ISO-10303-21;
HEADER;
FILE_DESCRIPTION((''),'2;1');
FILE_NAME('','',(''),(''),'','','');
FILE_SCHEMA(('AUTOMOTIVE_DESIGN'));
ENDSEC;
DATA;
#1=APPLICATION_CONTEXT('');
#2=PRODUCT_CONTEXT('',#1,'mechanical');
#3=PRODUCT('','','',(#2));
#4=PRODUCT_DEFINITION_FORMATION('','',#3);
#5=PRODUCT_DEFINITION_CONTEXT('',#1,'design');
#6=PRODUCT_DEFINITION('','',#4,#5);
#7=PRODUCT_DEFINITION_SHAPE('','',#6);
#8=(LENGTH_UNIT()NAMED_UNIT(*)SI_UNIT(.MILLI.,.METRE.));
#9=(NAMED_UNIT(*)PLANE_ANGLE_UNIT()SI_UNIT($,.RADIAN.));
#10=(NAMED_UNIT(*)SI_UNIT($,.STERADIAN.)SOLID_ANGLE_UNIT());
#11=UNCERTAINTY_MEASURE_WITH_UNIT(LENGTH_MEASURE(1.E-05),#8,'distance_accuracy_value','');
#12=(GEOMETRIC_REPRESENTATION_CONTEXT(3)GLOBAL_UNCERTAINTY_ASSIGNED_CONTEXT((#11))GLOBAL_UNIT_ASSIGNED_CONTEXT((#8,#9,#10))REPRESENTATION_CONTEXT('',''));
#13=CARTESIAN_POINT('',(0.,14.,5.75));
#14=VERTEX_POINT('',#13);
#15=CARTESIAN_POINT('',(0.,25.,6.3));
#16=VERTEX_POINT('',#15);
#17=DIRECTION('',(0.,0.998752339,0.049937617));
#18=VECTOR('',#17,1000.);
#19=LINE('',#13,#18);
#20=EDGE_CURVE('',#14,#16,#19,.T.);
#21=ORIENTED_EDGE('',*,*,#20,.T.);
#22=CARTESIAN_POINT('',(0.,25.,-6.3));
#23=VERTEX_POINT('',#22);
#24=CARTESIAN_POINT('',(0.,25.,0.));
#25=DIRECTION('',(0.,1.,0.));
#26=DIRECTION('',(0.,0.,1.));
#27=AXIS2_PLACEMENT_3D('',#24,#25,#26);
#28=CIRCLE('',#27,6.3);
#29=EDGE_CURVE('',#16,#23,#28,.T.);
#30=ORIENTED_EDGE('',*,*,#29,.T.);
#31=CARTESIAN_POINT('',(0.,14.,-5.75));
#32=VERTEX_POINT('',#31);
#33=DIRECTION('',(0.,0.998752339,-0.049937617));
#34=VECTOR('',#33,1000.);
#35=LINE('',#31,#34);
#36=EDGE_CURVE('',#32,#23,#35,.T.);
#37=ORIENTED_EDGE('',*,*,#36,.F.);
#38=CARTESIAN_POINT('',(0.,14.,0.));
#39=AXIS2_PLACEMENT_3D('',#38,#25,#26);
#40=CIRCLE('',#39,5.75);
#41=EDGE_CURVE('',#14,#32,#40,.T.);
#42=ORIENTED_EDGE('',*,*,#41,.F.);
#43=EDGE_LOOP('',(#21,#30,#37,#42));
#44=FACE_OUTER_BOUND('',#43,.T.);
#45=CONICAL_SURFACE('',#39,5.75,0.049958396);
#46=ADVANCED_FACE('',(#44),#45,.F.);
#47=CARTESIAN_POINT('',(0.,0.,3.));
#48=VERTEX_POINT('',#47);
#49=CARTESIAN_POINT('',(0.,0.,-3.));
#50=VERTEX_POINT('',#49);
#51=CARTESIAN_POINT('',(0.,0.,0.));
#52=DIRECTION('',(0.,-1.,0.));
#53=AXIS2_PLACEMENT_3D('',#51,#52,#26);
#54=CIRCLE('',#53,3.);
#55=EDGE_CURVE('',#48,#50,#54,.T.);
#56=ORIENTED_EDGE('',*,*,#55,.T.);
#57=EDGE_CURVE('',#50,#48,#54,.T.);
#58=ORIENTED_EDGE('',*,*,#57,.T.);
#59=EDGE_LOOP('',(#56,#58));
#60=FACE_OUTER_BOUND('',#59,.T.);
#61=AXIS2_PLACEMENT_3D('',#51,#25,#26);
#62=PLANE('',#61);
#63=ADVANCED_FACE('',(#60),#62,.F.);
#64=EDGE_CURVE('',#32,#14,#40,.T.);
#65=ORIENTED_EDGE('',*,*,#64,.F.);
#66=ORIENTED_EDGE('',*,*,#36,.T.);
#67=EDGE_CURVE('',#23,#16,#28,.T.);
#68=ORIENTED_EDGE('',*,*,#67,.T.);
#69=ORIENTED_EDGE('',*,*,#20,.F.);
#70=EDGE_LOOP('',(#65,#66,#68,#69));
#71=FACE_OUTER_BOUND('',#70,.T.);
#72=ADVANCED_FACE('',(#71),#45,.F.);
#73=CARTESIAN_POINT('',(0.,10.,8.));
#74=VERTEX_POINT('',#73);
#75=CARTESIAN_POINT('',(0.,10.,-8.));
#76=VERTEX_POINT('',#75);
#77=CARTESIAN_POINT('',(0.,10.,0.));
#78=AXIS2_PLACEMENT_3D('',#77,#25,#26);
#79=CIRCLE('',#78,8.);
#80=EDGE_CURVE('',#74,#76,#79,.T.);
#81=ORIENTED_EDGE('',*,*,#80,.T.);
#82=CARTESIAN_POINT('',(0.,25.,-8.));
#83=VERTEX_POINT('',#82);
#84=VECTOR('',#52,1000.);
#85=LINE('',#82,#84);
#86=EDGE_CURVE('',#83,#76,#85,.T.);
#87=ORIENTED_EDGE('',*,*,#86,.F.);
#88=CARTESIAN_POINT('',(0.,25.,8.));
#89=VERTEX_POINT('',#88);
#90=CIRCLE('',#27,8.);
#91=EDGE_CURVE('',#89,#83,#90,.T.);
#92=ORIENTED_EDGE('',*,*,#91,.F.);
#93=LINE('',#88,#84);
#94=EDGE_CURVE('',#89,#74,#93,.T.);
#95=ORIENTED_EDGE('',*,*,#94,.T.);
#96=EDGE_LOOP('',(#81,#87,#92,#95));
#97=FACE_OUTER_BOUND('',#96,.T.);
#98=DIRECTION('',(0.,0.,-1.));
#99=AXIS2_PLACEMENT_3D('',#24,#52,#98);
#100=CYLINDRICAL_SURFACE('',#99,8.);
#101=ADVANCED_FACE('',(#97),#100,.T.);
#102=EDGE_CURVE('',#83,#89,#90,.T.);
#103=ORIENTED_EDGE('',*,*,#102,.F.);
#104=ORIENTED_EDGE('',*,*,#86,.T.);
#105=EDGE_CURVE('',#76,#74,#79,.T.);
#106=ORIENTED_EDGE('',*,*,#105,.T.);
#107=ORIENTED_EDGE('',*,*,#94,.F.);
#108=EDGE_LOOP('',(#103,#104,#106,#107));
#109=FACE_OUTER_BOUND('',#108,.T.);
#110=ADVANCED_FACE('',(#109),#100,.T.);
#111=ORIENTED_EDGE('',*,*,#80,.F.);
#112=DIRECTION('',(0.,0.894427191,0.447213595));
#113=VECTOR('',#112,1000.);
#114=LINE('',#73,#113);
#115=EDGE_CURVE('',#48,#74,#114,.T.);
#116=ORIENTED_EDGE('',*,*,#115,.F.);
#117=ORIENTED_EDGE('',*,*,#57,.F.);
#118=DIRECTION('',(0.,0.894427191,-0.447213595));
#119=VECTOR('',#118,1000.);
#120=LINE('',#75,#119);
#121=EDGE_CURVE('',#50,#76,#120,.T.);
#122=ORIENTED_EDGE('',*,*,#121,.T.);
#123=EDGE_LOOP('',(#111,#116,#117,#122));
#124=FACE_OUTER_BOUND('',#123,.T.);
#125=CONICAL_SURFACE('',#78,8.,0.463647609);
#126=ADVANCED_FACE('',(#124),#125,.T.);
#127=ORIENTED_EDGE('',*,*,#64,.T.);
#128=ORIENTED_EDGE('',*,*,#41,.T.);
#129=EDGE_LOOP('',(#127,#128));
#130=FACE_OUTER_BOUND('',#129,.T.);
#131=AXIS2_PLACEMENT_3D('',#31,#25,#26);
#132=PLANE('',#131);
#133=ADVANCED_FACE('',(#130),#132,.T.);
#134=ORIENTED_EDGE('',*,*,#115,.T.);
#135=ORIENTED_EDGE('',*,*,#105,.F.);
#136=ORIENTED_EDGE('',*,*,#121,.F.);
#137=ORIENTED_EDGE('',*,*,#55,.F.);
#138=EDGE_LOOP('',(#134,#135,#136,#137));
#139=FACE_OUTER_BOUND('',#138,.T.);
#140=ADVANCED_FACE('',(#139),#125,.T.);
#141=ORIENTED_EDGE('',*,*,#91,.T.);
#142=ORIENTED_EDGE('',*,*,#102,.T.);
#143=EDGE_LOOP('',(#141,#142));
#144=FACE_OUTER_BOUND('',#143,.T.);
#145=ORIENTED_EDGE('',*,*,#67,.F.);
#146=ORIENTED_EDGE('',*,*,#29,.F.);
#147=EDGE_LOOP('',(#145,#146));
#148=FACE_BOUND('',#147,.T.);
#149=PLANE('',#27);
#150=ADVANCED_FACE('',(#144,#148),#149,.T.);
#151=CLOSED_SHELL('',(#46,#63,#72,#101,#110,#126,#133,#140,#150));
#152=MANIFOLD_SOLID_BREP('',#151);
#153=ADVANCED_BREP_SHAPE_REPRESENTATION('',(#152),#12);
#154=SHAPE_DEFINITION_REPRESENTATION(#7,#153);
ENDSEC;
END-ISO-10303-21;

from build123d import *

# Parameters (mm, degrees)
SKETCH_1_R      = 8
EXTRUDE_1_DEPTH = 25
CHAMFER_2_SIZE  = 5
CHAMFER_2_SIZE2 = 10


with BuildPart() as part:
    # 草图1 → 凸台-拉伸1 (new body)
    with BuildSketch(Plane(origin=(0, 0, 0), x_dir=(1, 0, 0), z_dir=(0, 1, 0))):
        with Locations(Location((0, 0, 0), (0, 0, 270))):
            Circle(SKETCH_1_R)
    extrude(amount=EXTRUDE_1_DEPTH)

    # 倒角2
    chamfer_2_edges = [part.edges().sort_by_distance(p)[0] for p in [
        (0, 0, -8),
    ]]
    chamfer_2_side = [part.faces().sort_by_distance(p)[0] for p in [
        (0, 0, 0),
    ]]
    chamfer(chamfer_2_edges, length=CHAMFER_2_SIZE, length2=CHAMFER_2_SIZE2, reference=chamfer_2_side[0])

    # 草图3 → 切除-旋转1 (revolve, cut)
    with BuildSketch(Plane(origin=(0, 0, 0), x_dir=(0, 0, -1), z_dir=(1, 0, 0)), mode=Mode.PRIVATE) as cut_revolve_1_sk:
        Polygon((6.3, 25), (5.75, 14), (0, 14), (0, 25), align=None)
    revolve(cut_revolve_1_sk.sketch.rotate(Axis((0, 25, 0), (0, -1, 0)), 180), axis=Axis((0, 25, 0), (0, -1, 0)), mode=Mode.SUBTRACT)


solid = part.part
